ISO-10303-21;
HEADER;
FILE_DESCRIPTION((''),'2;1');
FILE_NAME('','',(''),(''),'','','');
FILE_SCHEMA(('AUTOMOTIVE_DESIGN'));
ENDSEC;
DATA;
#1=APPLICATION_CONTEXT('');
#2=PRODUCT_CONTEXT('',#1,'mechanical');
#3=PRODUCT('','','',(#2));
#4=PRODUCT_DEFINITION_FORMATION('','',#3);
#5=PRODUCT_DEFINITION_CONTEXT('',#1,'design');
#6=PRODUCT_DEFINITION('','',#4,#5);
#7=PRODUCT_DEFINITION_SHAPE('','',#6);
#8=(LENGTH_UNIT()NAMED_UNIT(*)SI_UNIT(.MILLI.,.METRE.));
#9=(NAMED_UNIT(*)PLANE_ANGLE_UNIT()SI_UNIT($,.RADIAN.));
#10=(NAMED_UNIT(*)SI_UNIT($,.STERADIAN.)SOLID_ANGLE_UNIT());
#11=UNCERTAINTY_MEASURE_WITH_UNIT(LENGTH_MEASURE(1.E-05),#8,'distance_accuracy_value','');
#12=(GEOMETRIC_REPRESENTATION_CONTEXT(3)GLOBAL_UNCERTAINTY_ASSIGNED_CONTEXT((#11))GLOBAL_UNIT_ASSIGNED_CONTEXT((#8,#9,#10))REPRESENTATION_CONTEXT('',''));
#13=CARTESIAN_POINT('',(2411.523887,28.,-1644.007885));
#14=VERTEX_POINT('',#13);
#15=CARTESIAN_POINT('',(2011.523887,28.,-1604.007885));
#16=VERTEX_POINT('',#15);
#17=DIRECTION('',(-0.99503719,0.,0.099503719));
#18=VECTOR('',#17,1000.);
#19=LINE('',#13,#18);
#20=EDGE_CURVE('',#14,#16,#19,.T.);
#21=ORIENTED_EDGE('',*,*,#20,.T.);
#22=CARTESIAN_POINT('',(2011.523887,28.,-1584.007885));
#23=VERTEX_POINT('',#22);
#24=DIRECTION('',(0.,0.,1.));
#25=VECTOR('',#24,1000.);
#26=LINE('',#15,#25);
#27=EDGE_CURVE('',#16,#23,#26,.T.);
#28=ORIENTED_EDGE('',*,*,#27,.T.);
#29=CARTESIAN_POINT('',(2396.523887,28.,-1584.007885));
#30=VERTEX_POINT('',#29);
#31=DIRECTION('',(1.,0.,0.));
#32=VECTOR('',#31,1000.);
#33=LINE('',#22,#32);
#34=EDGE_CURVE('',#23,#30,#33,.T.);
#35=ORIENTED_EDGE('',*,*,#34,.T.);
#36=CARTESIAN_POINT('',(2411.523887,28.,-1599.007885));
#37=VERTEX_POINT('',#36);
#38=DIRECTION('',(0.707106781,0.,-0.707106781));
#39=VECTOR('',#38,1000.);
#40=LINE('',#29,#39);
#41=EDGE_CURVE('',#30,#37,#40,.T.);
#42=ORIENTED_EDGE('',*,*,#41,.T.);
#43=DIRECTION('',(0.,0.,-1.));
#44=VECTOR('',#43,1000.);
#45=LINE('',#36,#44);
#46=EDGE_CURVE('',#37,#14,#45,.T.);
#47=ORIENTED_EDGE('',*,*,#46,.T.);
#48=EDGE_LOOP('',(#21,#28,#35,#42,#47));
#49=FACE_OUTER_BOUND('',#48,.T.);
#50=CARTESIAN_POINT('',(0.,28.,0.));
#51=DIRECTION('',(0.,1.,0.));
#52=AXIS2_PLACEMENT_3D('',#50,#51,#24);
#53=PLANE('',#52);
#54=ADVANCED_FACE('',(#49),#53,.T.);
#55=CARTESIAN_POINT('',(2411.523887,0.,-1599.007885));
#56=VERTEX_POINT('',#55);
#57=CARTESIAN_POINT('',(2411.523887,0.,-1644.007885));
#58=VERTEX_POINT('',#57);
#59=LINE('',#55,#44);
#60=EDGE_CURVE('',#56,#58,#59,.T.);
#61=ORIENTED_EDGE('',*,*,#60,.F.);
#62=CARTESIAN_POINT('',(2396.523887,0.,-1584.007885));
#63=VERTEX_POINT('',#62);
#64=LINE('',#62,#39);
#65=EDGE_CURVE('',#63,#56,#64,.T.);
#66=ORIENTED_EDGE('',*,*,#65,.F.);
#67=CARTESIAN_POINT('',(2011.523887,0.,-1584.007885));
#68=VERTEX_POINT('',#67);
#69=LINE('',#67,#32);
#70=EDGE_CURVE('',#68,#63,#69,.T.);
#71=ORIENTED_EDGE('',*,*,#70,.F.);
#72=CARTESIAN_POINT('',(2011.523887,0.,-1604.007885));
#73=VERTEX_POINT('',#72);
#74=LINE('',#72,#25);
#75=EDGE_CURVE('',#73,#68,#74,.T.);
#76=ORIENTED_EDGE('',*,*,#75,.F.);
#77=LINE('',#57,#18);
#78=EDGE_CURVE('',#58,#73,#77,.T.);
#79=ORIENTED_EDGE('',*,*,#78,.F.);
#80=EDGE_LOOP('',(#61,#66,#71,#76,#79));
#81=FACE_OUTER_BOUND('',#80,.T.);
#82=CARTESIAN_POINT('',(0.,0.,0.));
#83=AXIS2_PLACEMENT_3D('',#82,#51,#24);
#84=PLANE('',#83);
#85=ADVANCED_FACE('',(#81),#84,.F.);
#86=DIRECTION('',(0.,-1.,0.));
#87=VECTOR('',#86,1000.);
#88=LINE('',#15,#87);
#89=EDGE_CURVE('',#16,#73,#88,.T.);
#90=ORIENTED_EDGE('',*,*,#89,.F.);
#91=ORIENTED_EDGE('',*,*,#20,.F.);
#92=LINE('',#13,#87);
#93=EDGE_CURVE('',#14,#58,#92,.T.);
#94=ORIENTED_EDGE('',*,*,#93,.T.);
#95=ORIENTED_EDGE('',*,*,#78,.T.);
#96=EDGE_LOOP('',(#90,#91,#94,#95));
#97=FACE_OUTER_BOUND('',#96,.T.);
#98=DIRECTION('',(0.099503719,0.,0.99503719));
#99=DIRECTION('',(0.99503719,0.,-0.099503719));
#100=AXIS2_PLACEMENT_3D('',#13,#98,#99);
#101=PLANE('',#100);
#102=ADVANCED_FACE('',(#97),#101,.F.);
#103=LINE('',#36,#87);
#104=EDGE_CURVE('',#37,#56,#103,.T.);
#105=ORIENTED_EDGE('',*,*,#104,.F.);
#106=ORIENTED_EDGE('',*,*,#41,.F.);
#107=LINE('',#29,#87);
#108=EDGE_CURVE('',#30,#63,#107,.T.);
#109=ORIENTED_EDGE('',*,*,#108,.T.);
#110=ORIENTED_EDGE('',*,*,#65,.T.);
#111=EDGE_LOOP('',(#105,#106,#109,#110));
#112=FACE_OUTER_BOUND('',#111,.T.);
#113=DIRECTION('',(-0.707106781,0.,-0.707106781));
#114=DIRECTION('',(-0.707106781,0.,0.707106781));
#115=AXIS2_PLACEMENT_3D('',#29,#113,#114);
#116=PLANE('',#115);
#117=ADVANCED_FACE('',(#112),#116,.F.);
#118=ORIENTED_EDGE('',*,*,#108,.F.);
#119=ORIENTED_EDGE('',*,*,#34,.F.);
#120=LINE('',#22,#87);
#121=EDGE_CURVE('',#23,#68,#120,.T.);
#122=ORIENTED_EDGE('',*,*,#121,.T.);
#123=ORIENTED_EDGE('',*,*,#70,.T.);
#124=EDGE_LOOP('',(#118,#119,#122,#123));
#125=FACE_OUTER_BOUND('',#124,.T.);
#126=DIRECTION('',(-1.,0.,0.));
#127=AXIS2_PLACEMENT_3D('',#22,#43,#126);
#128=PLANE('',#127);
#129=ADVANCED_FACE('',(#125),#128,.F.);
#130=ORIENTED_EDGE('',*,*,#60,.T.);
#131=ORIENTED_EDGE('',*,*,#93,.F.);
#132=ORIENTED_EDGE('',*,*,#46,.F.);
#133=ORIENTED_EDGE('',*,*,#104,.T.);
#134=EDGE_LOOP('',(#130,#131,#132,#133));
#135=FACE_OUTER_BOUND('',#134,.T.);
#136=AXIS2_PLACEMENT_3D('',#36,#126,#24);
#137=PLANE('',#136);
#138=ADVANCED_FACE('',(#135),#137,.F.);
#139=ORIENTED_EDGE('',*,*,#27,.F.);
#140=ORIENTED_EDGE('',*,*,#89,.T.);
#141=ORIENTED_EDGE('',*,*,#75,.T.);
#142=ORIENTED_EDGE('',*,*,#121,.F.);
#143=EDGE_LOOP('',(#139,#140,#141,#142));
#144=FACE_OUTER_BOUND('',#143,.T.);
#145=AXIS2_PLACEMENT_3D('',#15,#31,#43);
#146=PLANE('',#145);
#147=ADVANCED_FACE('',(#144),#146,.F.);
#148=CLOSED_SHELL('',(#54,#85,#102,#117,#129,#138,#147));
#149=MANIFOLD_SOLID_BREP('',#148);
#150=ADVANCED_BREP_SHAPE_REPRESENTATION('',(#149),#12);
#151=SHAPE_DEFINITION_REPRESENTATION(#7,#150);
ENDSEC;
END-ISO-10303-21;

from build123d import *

# Parameters (mm, degrees)
BOSS_EXTRUDE1_DEPTH = 28


with BuildPart() as part:
    # Sketch1 → Boss-Extrude1 (new body)
    with BuildSketch(Plane(origin=(0, 0, 0), x_dir=(1, 0, 0), z_dir=(0, 1, 0))):
        Polygon((2011.523887052, 1584.007884982), (2396.523887052, 1584.007884982), (2411.523887052, 1599.007884982), (2411.523887052, 1644.007884982), (2011.523887052, 1604.007884982), align=None)
    extrude(amount=BOSS_EXTRUDE1_DEPTH)


solid = part.part
